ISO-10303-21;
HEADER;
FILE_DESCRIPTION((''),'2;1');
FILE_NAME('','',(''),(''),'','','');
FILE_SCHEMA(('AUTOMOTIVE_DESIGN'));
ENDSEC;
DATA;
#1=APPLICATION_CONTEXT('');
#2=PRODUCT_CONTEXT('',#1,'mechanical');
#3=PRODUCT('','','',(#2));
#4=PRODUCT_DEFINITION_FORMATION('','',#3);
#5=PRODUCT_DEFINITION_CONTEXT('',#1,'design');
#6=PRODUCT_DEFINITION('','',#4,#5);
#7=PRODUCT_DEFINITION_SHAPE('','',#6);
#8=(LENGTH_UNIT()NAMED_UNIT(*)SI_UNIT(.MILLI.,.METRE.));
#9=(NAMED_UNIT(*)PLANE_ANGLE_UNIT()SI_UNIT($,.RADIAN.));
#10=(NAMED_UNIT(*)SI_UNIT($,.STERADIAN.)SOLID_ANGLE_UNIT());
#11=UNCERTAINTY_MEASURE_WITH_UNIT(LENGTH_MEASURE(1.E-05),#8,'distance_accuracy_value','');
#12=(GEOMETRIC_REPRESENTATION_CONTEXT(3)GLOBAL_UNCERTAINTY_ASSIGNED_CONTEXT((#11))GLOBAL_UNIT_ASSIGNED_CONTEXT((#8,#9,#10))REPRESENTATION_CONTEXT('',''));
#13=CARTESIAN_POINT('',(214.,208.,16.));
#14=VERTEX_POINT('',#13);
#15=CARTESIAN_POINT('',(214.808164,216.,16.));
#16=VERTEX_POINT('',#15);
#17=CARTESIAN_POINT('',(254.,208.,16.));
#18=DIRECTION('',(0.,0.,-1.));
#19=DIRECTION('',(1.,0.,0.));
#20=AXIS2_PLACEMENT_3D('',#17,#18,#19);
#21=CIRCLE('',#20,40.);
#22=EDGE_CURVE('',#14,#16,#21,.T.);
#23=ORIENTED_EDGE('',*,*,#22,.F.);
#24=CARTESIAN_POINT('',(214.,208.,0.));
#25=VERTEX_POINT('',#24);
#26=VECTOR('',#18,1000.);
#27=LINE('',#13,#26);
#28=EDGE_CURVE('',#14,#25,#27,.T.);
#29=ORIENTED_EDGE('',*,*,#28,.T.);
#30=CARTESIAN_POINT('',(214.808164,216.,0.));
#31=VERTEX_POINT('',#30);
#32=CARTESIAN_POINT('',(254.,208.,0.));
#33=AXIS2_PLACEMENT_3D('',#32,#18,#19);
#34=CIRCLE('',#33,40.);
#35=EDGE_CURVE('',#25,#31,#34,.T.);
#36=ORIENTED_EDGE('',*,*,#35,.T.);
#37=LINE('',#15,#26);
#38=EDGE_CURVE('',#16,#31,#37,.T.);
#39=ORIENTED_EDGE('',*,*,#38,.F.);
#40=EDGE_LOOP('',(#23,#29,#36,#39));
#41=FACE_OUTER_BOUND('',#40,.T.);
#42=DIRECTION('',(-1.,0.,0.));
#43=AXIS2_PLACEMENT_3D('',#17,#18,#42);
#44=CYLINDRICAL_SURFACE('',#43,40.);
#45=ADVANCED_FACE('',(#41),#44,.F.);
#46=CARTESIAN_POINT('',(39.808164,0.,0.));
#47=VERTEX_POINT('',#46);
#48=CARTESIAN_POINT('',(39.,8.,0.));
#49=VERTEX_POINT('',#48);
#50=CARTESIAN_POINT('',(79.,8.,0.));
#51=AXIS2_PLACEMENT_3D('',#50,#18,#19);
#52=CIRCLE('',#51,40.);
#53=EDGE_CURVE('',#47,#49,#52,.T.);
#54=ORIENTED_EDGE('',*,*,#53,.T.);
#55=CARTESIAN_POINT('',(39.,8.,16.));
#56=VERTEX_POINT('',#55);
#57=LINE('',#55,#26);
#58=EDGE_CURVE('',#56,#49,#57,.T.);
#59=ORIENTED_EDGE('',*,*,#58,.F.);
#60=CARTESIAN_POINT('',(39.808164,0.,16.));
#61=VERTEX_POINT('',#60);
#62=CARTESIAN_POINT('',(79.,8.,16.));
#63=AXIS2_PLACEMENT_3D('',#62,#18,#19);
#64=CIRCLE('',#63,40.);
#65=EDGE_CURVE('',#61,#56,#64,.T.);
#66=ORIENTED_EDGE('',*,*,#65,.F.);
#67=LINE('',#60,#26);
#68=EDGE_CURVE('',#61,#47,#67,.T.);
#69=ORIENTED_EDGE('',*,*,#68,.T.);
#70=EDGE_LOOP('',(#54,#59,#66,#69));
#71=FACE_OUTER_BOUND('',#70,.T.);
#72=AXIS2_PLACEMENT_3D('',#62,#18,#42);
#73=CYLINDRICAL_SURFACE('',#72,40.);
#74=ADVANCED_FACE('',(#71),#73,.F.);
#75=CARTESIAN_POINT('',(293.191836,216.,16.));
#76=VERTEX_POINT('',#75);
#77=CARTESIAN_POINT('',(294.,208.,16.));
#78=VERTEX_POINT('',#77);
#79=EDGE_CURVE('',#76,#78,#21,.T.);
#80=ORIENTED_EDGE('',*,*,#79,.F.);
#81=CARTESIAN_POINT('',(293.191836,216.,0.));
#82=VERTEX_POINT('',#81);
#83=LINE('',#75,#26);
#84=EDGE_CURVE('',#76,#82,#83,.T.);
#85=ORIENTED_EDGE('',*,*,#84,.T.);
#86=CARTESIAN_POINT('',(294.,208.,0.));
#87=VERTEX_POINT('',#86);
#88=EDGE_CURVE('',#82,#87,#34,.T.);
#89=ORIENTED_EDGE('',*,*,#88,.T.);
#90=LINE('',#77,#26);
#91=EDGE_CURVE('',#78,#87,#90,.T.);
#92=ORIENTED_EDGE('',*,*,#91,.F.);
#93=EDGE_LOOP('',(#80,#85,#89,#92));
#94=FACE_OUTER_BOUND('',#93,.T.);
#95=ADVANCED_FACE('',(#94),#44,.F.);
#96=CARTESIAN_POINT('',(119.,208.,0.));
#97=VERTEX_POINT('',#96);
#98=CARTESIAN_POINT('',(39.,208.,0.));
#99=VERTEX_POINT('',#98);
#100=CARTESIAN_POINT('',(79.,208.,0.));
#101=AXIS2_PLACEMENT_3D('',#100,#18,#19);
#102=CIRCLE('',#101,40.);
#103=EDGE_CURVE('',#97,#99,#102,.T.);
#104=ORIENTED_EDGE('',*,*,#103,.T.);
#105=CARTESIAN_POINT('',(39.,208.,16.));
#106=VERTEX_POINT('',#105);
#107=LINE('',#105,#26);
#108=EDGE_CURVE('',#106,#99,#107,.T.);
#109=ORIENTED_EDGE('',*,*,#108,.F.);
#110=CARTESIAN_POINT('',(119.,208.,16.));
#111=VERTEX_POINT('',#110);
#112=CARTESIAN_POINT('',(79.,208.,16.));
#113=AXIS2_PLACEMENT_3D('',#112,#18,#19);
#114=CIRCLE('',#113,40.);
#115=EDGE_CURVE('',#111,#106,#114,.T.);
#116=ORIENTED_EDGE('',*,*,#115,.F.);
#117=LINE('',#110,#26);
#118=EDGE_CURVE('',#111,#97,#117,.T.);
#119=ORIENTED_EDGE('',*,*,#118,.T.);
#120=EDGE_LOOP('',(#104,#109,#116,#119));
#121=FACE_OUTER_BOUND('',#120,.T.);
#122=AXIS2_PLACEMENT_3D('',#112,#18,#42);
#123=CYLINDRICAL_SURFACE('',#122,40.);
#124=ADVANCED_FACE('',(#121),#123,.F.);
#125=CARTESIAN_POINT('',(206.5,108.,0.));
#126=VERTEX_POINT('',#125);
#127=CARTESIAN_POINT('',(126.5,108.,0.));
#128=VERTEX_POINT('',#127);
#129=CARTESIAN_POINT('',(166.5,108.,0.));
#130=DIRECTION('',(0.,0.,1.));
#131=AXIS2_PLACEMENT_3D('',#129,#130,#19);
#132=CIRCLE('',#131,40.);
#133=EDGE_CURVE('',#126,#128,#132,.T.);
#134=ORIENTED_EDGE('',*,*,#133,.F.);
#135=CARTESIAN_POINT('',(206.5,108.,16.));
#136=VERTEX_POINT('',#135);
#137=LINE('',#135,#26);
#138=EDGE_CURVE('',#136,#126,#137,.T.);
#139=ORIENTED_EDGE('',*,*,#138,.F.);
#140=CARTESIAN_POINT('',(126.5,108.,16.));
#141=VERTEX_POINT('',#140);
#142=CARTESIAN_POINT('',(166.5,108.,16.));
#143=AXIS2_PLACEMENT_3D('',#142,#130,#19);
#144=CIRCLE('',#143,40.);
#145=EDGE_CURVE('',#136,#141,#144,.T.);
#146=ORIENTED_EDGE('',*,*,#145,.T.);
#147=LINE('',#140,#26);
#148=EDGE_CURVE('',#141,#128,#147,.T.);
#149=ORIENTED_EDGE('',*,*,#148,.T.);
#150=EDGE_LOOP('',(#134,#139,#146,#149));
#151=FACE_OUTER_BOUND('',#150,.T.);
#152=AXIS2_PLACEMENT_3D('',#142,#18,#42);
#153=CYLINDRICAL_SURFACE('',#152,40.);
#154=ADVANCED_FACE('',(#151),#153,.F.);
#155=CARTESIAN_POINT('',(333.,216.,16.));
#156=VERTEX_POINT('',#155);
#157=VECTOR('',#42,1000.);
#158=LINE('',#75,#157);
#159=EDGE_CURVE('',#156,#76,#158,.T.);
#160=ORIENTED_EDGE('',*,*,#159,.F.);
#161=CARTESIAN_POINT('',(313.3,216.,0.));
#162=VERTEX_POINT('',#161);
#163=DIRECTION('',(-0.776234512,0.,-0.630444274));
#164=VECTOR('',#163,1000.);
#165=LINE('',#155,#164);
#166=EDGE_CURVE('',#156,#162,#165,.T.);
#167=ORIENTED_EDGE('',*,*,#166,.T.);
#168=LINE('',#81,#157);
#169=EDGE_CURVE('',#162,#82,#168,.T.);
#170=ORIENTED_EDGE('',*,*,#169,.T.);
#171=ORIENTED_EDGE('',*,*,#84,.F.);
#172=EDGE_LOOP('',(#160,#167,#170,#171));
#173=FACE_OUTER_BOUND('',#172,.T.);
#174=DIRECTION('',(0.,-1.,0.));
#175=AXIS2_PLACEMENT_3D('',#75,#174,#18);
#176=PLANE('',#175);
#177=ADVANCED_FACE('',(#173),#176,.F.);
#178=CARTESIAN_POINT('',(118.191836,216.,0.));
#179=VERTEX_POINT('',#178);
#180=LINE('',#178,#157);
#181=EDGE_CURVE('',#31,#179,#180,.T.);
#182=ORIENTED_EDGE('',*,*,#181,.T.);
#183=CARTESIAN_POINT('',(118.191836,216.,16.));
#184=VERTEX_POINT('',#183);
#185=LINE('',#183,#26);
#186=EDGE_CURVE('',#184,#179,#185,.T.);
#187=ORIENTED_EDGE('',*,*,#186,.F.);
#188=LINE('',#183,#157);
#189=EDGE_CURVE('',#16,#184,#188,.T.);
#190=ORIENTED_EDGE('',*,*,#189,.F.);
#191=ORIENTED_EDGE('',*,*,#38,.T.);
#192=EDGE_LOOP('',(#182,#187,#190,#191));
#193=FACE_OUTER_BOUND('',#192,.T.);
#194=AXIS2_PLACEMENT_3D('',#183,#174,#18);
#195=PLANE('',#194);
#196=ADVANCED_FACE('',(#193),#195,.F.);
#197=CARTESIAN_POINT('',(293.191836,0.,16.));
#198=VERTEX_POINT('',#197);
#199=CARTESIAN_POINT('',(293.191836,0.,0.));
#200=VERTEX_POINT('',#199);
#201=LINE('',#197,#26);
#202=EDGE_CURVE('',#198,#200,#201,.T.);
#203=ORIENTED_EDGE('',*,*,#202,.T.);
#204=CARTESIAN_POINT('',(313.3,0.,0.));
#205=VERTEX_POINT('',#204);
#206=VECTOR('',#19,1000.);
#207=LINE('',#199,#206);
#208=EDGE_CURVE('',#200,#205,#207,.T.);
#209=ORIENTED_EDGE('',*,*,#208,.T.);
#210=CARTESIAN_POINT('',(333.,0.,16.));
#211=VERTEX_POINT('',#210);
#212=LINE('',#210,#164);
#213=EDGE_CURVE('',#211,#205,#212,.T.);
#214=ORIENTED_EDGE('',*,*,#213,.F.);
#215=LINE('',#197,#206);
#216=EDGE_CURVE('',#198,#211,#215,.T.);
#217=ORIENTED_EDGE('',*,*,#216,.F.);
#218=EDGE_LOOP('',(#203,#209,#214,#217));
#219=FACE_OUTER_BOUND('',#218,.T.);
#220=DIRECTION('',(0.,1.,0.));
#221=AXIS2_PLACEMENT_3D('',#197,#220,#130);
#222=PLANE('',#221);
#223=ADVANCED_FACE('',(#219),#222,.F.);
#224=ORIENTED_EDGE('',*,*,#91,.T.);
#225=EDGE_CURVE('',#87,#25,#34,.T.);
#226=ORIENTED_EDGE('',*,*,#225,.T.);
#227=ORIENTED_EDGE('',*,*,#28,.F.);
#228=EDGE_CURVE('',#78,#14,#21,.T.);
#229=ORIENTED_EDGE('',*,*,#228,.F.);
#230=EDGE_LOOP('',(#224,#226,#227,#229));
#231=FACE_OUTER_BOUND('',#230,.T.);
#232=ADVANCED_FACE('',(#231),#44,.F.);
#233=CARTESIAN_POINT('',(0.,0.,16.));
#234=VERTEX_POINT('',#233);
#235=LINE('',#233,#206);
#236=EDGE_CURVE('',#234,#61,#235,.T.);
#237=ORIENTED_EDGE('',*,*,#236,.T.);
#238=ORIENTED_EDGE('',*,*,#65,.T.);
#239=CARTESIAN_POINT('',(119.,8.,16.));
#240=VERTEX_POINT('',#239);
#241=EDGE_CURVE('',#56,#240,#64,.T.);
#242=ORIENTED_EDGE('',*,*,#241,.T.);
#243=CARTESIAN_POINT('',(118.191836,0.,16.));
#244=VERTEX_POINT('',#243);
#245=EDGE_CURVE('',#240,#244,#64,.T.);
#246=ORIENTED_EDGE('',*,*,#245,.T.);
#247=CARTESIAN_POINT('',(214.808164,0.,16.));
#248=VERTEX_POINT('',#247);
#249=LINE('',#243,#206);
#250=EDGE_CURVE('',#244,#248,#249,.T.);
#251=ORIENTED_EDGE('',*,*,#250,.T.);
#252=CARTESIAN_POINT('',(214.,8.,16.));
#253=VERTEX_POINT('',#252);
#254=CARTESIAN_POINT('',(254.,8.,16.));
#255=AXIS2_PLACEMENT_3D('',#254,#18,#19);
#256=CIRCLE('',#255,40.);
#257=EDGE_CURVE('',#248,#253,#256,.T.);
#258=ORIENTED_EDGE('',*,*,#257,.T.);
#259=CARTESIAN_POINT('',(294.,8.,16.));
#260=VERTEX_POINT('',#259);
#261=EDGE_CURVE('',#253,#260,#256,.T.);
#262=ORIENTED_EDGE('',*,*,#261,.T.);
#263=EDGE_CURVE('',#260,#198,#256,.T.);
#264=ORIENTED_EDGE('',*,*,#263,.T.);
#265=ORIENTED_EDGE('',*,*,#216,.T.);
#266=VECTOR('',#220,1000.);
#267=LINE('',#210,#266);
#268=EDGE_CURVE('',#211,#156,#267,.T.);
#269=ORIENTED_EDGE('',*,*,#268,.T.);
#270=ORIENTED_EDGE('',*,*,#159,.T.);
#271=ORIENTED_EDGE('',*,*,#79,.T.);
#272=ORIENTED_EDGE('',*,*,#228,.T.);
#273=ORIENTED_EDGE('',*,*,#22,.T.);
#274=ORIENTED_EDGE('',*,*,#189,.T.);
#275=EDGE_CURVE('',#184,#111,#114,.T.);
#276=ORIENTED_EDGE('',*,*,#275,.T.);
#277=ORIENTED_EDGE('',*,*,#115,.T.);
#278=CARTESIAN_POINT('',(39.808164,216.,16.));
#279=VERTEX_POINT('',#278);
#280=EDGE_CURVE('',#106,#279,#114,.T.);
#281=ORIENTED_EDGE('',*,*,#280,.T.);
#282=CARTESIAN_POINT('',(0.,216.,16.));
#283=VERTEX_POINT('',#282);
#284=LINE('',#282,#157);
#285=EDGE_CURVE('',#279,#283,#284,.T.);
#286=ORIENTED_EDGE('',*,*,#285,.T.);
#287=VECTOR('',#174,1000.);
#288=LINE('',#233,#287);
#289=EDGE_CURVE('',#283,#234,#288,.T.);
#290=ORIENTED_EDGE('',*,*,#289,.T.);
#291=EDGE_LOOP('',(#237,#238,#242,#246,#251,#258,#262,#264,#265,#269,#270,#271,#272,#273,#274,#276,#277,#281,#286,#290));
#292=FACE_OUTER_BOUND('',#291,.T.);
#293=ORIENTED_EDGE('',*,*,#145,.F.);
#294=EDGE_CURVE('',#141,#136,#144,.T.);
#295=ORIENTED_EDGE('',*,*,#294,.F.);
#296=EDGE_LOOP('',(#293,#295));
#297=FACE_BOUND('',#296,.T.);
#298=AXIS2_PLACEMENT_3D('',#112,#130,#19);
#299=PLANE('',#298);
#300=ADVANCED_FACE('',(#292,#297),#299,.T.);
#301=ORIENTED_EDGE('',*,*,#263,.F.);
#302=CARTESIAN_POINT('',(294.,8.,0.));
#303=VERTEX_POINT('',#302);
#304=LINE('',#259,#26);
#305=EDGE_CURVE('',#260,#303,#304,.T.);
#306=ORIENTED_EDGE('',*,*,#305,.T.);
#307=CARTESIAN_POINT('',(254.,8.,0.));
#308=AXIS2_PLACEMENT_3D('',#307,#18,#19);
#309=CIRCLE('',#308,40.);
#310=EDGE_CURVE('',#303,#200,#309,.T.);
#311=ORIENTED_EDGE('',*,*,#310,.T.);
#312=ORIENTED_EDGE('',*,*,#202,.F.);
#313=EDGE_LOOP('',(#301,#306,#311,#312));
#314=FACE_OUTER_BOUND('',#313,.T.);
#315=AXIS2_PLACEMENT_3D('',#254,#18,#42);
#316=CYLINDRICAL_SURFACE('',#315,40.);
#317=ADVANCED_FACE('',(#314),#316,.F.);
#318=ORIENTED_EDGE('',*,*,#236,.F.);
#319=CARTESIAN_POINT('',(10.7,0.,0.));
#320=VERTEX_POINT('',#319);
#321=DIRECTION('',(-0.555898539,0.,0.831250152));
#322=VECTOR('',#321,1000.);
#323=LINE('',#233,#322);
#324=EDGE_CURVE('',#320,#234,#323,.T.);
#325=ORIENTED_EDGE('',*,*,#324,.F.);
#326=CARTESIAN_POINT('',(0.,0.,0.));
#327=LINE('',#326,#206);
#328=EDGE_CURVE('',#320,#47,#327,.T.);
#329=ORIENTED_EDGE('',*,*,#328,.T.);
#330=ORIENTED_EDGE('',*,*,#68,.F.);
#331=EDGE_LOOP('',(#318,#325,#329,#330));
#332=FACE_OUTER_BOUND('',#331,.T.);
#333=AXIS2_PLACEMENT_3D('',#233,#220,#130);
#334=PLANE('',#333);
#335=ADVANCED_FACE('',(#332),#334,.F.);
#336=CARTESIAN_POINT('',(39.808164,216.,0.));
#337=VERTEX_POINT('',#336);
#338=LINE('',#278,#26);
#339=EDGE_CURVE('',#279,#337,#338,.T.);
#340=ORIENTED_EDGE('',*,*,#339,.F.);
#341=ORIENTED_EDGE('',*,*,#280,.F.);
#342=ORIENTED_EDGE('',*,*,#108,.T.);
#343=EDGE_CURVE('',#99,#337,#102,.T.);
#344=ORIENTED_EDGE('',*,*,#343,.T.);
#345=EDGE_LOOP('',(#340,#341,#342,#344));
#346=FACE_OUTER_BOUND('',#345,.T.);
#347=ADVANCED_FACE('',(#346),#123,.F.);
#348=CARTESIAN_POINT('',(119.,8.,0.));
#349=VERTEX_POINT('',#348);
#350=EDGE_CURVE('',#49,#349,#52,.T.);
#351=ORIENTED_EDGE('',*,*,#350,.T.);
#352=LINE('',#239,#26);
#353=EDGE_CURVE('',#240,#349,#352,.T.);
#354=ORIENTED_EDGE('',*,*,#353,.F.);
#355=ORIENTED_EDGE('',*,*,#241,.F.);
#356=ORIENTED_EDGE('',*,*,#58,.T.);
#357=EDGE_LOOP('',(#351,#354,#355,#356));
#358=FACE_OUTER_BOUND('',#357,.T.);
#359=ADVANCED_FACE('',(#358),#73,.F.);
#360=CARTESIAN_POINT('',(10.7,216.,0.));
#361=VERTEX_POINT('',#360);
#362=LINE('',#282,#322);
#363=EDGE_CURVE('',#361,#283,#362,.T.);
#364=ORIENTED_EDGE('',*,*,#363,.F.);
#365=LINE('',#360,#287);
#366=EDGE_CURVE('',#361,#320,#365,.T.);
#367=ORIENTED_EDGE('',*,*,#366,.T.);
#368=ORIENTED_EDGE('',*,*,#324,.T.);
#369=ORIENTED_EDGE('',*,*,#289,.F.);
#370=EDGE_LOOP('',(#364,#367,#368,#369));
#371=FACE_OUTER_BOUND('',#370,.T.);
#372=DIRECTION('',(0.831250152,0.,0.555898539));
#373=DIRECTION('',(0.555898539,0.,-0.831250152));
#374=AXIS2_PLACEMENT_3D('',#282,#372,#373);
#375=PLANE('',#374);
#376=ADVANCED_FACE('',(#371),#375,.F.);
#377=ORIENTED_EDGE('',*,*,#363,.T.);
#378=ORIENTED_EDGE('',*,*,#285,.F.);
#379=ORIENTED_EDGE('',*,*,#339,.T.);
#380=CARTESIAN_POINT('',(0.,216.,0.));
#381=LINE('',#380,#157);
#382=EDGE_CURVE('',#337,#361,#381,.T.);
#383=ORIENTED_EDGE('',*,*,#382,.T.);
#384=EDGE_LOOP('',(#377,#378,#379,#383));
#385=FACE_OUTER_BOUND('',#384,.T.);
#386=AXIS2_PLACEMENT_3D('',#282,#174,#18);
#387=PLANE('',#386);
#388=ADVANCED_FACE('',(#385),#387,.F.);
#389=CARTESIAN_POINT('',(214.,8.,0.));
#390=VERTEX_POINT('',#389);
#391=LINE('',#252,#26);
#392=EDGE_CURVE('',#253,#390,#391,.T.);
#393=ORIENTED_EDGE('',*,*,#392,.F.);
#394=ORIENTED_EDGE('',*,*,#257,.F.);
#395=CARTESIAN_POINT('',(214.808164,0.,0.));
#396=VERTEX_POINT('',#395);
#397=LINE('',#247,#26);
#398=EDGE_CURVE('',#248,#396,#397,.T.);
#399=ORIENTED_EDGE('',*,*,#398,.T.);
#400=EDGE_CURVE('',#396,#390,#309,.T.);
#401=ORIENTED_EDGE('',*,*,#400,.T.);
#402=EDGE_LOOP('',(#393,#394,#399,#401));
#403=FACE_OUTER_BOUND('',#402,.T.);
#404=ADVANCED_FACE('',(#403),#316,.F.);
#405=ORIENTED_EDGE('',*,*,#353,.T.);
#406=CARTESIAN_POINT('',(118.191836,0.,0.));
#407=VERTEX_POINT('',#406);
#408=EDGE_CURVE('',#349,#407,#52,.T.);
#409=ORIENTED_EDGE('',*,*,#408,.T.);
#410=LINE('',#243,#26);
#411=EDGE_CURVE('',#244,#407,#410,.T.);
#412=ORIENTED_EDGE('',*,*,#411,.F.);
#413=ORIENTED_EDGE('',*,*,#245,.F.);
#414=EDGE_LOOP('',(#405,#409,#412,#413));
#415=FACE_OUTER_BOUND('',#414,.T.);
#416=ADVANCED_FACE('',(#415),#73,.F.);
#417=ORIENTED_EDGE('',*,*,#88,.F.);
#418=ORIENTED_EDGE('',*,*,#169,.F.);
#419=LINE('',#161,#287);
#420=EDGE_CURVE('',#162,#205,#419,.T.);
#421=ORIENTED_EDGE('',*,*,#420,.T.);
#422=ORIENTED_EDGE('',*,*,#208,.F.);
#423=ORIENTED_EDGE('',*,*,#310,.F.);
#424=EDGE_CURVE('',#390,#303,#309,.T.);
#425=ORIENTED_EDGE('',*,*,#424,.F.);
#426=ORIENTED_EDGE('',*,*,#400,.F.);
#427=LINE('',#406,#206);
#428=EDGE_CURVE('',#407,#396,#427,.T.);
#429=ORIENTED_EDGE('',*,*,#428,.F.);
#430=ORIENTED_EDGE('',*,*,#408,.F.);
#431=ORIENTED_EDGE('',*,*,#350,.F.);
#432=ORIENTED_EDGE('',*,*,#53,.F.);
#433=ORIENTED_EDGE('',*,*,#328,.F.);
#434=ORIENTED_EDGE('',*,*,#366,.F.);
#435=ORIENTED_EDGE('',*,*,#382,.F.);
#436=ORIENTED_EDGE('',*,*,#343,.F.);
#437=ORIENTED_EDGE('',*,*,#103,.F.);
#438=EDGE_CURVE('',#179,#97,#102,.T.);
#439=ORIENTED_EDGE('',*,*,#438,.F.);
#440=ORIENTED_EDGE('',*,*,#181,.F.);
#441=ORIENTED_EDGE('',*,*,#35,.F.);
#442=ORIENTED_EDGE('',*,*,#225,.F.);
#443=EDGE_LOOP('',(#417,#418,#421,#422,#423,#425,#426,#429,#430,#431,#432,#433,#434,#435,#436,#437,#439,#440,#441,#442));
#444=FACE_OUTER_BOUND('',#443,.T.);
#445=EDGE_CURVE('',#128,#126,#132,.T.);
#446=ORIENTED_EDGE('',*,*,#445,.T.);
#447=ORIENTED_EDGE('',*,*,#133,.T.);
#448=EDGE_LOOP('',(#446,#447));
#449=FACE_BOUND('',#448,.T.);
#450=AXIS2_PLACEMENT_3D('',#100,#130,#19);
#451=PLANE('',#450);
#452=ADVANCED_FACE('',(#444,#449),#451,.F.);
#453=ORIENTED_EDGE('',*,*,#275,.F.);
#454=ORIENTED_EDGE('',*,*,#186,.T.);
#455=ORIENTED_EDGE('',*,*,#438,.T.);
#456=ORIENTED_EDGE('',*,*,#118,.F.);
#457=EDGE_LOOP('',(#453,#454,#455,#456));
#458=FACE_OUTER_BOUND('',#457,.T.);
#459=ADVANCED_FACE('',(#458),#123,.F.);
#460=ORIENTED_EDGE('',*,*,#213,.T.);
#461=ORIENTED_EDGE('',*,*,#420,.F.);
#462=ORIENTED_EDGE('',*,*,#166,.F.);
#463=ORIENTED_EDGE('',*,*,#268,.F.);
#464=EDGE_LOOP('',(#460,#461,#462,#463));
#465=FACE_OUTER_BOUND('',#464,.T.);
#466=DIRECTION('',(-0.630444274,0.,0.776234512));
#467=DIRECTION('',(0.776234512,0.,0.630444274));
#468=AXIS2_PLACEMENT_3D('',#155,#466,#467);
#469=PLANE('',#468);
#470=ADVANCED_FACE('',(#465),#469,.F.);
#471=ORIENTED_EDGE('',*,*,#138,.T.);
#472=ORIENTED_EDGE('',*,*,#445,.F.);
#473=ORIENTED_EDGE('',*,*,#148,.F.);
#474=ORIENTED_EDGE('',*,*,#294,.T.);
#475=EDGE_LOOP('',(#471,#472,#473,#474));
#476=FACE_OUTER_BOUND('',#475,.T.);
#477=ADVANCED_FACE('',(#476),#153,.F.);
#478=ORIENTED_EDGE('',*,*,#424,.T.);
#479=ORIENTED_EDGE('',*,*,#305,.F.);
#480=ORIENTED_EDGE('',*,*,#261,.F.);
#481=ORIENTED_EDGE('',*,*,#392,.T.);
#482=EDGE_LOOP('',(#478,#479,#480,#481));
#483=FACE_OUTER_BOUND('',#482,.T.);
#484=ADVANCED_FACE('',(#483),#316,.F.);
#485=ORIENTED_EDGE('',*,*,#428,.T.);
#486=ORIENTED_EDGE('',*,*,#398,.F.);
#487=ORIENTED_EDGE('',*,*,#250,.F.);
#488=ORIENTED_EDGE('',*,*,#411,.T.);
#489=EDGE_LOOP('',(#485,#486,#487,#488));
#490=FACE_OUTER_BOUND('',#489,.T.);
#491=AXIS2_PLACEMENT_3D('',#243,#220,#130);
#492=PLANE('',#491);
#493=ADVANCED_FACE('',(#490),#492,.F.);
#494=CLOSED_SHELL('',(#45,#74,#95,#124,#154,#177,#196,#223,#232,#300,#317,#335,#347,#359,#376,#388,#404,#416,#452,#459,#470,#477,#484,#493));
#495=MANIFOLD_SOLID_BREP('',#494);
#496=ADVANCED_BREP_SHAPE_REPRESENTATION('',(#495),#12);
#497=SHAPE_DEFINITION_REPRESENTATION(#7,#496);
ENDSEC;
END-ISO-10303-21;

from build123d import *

# Parameters (mm, degrees)
SKETCH1_R           = 40
BOSS_EXTRUDE1_DEPTH = 16
CUT_EXTRUDE1_DEPTH  = 398.241740002


with BuildPart() as part:
    # Sketch1 → Boss-Extrude1 (new body)
    with BuildSketch(Plane.XY):
        with BuildLine():
            Line((0, 0), (39.808164115, 0))
            ThreePointArc((39.808164115, 0), (79, 48), (118.191835885, 0))
            Line((118.191835885, 0), (214.808164115, 0))
            ThreePointArc((214.808164115, 0), (254, 48), (293.191835885, 0))
            Line((293.191835885, 0), (333, 0))
            Line((333, 0), (333, 216))
            Line((333, 216), (293.191835885, 216))
            ThreePointArc((293.191835885, 216), (254, 168), (214.808164115, 216))
            Line((214.808164115, 216), (118.191835885, 216))
            ThreePointArc((118.191835885, 216), (79, 168), (39.808164115, 216))
            Line((39.808164115, 216), (0, 216))
            Line((0, 216), (0, 0))
        make_face()
        with Locations((166.5, 108)):
            Circle(SKETCH1_R, mode=Mode.SUBTRACT)
    extrude(amount=BOSS_EXTRUDE1_DEPTH)

    # Sketch2 → Cut-Extrude1 (cut, through all)
    with BuildSketch(Plane.XZ):
        Polygon((0, 16), (10.7, 0), (0, 0), align=None)
        Polygon((333, 16), (313.3, 0), (333, 0), align=None)
    extrude(amount=-CUT_EXTRUDE1_DEPTH, mode=Mode.SUBTRACT)


solid = part.part
